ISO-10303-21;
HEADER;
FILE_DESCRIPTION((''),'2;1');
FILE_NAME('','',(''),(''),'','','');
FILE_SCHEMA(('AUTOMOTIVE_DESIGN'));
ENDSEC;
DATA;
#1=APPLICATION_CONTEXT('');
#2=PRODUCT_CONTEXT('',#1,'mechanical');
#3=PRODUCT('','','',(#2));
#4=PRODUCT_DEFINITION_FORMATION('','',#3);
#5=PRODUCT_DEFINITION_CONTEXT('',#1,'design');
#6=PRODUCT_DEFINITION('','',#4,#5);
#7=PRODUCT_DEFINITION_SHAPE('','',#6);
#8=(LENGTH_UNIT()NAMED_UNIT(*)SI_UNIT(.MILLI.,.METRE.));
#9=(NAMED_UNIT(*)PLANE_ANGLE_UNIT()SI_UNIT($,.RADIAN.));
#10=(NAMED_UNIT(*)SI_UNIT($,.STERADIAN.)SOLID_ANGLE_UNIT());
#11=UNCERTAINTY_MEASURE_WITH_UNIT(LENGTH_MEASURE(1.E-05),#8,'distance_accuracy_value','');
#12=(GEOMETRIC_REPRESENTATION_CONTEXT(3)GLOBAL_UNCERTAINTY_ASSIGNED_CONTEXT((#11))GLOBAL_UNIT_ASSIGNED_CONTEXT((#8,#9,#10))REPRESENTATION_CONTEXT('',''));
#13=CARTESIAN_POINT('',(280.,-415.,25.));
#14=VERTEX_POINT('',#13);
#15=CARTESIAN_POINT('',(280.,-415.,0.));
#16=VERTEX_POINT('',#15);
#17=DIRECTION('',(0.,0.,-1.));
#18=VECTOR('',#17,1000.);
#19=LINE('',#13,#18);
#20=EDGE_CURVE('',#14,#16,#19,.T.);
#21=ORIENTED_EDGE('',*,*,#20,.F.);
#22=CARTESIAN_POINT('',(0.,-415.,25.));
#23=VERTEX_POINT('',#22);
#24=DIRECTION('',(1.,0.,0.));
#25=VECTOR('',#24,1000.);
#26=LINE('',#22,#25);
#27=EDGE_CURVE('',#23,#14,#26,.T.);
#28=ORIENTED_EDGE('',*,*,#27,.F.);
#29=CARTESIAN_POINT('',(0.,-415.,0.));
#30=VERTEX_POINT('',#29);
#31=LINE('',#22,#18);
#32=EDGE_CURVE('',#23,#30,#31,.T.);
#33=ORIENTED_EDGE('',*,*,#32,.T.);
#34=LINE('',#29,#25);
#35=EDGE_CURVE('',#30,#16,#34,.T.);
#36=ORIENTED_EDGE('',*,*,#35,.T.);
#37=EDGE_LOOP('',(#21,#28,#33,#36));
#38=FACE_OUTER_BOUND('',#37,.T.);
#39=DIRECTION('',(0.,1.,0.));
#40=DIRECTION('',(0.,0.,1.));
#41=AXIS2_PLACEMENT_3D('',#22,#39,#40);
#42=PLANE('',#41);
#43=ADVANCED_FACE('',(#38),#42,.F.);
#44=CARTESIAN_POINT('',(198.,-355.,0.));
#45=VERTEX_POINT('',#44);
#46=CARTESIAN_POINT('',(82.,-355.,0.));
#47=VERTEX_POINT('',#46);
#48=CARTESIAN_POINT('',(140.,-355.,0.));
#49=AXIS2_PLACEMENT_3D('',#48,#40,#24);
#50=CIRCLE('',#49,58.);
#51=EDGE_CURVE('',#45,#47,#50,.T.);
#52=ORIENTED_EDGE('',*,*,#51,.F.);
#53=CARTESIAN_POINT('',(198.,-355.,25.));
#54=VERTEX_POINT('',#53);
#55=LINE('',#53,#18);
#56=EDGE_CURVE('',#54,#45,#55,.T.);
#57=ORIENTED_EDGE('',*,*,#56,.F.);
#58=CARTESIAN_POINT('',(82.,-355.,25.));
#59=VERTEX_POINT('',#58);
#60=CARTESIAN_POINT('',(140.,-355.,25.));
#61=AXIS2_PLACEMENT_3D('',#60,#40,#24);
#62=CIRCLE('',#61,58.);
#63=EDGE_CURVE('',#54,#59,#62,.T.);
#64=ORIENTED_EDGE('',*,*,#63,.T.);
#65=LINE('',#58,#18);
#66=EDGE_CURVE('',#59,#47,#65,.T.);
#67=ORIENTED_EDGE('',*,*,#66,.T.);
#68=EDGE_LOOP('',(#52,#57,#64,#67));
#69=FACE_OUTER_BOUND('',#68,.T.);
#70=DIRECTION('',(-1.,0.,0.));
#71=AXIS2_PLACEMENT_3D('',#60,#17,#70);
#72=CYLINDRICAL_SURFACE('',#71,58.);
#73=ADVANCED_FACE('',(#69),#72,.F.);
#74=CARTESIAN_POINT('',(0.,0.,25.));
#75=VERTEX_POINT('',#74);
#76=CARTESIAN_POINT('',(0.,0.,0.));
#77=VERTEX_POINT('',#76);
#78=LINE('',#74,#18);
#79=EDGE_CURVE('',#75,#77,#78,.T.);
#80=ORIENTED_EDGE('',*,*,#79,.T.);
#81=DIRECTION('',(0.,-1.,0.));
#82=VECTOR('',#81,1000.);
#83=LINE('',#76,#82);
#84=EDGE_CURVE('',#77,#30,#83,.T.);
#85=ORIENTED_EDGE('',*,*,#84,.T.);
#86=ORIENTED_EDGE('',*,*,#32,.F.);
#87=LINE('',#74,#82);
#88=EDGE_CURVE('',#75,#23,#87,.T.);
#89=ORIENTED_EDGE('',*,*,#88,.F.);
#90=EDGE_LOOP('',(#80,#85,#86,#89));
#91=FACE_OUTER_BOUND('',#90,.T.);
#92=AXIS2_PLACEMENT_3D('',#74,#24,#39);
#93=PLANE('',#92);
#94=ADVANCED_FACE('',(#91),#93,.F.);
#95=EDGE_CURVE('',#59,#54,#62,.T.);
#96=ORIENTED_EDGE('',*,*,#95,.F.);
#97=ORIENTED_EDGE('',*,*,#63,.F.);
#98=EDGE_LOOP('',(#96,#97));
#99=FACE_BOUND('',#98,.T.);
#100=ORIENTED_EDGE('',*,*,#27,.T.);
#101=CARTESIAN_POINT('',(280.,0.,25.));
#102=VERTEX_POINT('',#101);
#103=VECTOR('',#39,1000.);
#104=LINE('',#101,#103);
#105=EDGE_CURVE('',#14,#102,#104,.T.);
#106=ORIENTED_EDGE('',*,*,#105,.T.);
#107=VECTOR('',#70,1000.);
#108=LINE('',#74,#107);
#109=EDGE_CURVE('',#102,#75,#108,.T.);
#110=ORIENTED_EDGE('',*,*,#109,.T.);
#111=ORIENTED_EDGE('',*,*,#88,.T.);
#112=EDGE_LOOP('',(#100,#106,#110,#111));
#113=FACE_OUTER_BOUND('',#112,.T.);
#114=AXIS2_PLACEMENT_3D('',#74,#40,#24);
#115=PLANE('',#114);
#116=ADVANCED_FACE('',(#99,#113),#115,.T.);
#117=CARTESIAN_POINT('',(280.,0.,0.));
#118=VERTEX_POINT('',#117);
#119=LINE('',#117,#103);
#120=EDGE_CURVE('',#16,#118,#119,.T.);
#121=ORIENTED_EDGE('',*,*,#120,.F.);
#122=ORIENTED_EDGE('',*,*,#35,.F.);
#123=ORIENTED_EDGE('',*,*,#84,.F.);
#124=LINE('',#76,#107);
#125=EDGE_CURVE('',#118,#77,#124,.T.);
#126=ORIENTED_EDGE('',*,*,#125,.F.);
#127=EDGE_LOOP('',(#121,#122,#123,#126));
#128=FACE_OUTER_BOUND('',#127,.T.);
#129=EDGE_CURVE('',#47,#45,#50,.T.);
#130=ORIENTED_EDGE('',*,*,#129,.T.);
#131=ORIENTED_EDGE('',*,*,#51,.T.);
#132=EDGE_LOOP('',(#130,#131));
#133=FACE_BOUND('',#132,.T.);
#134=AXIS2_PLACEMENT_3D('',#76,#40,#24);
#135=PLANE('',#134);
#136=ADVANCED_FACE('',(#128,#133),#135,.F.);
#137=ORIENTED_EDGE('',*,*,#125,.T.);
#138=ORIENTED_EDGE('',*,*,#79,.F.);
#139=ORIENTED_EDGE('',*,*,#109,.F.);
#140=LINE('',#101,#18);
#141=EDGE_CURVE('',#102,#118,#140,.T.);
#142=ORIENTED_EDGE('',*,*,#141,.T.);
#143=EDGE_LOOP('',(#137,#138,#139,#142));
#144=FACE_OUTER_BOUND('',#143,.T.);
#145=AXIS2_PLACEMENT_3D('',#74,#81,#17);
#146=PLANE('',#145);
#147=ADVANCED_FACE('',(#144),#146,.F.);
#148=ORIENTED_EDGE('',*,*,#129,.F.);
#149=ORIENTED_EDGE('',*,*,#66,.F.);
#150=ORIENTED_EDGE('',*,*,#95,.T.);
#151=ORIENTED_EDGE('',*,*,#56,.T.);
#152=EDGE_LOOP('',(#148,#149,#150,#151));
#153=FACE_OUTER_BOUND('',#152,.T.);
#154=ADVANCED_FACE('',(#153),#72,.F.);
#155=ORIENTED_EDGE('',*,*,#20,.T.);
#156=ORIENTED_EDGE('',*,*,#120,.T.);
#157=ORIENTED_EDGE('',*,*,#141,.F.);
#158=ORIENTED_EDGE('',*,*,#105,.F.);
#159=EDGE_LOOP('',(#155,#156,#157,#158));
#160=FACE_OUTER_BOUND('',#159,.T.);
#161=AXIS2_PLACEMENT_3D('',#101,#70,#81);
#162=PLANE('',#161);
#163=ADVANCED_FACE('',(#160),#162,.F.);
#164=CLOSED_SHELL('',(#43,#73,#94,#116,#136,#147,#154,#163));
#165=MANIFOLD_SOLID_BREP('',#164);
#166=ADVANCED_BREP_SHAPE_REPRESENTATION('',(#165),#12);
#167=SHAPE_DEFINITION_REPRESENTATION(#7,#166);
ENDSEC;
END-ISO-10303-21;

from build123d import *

# Parameters (mm, degrees)
SKETCH1_W           = 280
SKETCH1_H           = 415
SKETCH1_R           = 58
BOSS_EXTRUDE1_DEPTH = 25


with BuildPart() as part:
    # Sketch1 → Boss-Extrude1 (new body)
    with BuildSketch(Plane.XY):
        with Locations((140, -207.5)):
            Rectangle(SKETCH1_W, SKETCH1_H)
        with Locations((140, -355)):
            Circle(SKETCH1_R, mode=Mode.SUBTRACT)
    extrude(amount=BOSS_EXTRUDE1_DEPTH)


solid = part.part
